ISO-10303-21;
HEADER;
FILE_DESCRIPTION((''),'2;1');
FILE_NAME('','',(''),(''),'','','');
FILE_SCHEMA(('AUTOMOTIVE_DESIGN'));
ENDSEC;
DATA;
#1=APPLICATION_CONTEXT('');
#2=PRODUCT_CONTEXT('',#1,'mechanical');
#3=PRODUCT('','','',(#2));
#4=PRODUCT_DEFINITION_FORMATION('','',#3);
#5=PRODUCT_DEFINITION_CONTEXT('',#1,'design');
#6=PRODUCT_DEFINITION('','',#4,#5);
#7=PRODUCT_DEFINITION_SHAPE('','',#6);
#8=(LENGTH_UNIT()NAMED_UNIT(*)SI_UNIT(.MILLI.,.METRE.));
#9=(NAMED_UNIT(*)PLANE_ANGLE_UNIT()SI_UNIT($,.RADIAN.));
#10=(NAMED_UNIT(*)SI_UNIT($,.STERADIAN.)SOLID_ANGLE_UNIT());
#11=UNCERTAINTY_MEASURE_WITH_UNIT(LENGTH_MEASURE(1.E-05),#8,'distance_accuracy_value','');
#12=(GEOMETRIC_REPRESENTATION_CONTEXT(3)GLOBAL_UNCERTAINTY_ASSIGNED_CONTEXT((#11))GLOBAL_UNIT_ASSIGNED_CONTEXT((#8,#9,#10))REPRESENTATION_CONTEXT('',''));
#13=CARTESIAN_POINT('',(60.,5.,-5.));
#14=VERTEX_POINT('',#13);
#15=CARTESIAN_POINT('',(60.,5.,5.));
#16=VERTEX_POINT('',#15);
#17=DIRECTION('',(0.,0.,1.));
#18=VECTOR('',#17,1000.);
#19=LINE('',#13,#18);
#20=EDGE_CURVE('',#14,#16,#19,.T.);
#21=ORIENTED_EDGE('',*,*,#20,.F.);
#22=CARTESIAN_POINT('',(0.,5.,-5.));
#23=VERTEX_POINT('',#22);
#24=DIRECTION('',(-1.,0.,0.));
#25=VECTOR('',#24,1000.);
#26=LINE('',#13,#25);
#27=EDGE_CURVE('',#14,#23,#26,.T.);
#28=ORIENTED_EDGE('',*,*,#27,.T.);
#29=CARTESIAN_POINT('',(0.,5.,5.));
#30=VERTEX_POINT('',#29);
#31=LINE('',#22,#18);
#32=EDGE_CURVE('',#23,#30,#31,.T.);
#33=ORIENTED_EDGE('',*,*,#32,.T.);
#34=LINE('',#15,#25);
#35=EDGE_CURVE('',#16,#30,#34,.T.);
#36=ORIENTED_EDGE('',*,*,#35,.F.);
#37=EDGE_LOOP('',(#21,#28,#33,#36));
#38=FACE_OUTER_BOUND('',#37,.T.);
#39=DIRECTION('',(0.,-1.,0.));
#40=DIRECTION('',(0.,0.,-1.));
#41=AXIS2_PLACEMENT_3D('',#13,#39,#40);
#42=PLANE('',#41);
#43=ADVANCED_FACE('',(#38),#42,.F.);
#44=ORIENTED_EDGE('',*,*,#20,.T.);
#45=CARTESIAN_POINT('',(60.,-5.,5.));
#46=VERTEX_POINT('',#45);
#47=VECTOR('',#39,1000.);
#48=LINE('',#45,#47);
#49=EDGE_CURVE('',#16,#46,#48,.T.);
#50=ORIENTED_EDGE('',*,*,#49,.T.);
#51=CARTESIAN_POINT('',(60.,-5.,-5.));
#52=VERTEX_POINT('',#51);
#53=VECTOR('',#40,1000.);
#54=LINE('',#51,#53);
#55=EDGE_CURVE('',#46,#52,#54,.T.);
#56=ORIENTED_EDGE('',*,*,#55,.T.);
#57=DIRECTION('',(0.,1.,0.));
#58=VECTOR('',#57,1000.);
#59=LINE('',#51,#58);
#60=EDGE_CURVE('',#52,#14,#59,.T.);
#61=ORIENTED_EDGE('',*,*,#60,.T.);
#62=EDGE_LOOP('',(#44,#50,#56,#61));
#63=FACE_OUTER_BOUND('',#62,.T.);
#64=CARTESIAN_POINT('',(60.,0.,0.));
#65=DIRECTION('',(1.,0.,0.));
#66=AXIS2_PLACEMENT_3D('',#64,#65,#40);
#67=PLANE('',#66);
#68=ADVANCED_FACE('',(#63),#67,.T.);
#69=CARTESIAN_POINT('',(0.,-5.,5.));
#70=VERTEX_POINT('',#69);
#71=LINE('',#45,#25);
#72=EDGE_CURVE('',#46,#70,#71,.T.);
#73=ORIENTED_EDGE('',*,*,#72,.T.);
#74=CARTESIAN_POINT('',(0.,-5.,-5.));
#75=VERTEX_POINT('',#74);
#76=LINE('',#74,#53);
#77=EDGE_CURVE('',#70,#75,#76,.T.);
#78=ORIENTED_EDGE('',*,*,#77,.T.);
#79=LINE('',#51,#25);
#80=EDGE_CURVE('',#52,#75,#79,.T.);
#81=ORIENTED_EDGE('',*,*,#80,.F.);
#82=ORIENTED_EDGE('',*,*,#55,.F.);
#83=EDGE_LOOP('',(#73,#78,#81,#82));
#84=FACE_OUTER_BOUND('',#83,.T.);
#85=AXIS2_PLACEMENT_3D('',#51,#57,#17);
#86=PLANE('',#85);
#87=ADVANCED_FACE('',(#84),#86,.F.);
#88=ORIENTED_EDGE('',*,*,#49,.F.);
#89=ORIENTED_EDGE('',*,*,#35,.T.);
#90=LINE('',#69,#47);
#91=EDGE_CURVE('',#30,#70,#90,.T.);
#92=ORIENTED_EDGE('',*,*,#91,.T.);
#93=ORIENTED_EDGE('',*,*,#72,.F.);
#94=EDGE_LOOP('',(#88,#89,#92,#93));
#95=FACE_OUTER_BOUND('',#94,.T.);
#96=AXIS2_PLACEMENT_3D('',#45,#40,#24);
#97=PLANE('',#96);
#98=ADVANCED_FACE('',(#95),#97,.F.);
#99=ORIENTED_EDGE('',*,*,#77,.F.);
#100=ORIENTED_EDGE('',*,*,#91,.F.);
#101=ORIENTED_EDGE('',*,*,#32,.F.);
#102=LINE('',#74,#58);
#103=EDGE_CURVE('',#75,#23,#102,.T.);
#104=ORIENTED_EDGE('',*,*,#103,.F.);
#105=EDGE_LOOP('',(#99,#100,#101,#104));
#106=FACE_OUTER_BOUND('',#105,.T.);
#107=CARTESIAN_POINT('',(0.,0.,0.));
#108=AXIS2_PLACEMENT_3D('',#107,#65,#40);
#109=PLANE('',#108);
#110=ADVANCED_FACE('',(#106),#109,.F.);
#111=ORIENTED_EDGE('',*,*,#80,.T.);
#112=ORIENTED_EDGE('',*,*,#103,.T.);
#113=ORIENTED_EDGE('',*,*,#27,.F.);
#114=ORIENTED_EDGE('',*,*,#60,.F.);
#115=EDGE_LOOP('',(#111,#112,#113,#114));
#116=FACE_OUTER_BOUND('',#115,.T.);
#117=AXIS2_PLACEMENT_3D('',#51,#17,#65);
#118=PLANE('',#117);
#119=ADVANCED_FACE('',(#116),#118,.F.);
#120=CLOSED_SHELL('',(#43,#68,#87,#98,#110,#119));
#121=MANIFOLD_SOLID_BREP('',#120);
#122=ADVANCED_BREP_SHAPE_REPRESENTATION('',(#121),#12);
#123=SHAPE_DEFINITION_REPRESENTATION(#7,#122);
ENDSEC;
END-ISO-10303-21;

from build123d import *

# Parameters (mm, degrees)
SKETCH_1_W      = 10
SKETCH_1_H      = 10
EXTRUDE_1_DEPTH = 60


with BuildPart() as part:
    # 草图1 → 凸台-拉伸1 (new body)
    with BuildSketch(Plane(origin=(0, 0, 0), x_dir=(0, 0, -1), z_dir=(1, 0, 0))):
        Rectangle(SKETCH_1_W, SKETCH_1_H)
    extrude(amount=EXTRUDE_1_DEPTH)


solid = part.part
